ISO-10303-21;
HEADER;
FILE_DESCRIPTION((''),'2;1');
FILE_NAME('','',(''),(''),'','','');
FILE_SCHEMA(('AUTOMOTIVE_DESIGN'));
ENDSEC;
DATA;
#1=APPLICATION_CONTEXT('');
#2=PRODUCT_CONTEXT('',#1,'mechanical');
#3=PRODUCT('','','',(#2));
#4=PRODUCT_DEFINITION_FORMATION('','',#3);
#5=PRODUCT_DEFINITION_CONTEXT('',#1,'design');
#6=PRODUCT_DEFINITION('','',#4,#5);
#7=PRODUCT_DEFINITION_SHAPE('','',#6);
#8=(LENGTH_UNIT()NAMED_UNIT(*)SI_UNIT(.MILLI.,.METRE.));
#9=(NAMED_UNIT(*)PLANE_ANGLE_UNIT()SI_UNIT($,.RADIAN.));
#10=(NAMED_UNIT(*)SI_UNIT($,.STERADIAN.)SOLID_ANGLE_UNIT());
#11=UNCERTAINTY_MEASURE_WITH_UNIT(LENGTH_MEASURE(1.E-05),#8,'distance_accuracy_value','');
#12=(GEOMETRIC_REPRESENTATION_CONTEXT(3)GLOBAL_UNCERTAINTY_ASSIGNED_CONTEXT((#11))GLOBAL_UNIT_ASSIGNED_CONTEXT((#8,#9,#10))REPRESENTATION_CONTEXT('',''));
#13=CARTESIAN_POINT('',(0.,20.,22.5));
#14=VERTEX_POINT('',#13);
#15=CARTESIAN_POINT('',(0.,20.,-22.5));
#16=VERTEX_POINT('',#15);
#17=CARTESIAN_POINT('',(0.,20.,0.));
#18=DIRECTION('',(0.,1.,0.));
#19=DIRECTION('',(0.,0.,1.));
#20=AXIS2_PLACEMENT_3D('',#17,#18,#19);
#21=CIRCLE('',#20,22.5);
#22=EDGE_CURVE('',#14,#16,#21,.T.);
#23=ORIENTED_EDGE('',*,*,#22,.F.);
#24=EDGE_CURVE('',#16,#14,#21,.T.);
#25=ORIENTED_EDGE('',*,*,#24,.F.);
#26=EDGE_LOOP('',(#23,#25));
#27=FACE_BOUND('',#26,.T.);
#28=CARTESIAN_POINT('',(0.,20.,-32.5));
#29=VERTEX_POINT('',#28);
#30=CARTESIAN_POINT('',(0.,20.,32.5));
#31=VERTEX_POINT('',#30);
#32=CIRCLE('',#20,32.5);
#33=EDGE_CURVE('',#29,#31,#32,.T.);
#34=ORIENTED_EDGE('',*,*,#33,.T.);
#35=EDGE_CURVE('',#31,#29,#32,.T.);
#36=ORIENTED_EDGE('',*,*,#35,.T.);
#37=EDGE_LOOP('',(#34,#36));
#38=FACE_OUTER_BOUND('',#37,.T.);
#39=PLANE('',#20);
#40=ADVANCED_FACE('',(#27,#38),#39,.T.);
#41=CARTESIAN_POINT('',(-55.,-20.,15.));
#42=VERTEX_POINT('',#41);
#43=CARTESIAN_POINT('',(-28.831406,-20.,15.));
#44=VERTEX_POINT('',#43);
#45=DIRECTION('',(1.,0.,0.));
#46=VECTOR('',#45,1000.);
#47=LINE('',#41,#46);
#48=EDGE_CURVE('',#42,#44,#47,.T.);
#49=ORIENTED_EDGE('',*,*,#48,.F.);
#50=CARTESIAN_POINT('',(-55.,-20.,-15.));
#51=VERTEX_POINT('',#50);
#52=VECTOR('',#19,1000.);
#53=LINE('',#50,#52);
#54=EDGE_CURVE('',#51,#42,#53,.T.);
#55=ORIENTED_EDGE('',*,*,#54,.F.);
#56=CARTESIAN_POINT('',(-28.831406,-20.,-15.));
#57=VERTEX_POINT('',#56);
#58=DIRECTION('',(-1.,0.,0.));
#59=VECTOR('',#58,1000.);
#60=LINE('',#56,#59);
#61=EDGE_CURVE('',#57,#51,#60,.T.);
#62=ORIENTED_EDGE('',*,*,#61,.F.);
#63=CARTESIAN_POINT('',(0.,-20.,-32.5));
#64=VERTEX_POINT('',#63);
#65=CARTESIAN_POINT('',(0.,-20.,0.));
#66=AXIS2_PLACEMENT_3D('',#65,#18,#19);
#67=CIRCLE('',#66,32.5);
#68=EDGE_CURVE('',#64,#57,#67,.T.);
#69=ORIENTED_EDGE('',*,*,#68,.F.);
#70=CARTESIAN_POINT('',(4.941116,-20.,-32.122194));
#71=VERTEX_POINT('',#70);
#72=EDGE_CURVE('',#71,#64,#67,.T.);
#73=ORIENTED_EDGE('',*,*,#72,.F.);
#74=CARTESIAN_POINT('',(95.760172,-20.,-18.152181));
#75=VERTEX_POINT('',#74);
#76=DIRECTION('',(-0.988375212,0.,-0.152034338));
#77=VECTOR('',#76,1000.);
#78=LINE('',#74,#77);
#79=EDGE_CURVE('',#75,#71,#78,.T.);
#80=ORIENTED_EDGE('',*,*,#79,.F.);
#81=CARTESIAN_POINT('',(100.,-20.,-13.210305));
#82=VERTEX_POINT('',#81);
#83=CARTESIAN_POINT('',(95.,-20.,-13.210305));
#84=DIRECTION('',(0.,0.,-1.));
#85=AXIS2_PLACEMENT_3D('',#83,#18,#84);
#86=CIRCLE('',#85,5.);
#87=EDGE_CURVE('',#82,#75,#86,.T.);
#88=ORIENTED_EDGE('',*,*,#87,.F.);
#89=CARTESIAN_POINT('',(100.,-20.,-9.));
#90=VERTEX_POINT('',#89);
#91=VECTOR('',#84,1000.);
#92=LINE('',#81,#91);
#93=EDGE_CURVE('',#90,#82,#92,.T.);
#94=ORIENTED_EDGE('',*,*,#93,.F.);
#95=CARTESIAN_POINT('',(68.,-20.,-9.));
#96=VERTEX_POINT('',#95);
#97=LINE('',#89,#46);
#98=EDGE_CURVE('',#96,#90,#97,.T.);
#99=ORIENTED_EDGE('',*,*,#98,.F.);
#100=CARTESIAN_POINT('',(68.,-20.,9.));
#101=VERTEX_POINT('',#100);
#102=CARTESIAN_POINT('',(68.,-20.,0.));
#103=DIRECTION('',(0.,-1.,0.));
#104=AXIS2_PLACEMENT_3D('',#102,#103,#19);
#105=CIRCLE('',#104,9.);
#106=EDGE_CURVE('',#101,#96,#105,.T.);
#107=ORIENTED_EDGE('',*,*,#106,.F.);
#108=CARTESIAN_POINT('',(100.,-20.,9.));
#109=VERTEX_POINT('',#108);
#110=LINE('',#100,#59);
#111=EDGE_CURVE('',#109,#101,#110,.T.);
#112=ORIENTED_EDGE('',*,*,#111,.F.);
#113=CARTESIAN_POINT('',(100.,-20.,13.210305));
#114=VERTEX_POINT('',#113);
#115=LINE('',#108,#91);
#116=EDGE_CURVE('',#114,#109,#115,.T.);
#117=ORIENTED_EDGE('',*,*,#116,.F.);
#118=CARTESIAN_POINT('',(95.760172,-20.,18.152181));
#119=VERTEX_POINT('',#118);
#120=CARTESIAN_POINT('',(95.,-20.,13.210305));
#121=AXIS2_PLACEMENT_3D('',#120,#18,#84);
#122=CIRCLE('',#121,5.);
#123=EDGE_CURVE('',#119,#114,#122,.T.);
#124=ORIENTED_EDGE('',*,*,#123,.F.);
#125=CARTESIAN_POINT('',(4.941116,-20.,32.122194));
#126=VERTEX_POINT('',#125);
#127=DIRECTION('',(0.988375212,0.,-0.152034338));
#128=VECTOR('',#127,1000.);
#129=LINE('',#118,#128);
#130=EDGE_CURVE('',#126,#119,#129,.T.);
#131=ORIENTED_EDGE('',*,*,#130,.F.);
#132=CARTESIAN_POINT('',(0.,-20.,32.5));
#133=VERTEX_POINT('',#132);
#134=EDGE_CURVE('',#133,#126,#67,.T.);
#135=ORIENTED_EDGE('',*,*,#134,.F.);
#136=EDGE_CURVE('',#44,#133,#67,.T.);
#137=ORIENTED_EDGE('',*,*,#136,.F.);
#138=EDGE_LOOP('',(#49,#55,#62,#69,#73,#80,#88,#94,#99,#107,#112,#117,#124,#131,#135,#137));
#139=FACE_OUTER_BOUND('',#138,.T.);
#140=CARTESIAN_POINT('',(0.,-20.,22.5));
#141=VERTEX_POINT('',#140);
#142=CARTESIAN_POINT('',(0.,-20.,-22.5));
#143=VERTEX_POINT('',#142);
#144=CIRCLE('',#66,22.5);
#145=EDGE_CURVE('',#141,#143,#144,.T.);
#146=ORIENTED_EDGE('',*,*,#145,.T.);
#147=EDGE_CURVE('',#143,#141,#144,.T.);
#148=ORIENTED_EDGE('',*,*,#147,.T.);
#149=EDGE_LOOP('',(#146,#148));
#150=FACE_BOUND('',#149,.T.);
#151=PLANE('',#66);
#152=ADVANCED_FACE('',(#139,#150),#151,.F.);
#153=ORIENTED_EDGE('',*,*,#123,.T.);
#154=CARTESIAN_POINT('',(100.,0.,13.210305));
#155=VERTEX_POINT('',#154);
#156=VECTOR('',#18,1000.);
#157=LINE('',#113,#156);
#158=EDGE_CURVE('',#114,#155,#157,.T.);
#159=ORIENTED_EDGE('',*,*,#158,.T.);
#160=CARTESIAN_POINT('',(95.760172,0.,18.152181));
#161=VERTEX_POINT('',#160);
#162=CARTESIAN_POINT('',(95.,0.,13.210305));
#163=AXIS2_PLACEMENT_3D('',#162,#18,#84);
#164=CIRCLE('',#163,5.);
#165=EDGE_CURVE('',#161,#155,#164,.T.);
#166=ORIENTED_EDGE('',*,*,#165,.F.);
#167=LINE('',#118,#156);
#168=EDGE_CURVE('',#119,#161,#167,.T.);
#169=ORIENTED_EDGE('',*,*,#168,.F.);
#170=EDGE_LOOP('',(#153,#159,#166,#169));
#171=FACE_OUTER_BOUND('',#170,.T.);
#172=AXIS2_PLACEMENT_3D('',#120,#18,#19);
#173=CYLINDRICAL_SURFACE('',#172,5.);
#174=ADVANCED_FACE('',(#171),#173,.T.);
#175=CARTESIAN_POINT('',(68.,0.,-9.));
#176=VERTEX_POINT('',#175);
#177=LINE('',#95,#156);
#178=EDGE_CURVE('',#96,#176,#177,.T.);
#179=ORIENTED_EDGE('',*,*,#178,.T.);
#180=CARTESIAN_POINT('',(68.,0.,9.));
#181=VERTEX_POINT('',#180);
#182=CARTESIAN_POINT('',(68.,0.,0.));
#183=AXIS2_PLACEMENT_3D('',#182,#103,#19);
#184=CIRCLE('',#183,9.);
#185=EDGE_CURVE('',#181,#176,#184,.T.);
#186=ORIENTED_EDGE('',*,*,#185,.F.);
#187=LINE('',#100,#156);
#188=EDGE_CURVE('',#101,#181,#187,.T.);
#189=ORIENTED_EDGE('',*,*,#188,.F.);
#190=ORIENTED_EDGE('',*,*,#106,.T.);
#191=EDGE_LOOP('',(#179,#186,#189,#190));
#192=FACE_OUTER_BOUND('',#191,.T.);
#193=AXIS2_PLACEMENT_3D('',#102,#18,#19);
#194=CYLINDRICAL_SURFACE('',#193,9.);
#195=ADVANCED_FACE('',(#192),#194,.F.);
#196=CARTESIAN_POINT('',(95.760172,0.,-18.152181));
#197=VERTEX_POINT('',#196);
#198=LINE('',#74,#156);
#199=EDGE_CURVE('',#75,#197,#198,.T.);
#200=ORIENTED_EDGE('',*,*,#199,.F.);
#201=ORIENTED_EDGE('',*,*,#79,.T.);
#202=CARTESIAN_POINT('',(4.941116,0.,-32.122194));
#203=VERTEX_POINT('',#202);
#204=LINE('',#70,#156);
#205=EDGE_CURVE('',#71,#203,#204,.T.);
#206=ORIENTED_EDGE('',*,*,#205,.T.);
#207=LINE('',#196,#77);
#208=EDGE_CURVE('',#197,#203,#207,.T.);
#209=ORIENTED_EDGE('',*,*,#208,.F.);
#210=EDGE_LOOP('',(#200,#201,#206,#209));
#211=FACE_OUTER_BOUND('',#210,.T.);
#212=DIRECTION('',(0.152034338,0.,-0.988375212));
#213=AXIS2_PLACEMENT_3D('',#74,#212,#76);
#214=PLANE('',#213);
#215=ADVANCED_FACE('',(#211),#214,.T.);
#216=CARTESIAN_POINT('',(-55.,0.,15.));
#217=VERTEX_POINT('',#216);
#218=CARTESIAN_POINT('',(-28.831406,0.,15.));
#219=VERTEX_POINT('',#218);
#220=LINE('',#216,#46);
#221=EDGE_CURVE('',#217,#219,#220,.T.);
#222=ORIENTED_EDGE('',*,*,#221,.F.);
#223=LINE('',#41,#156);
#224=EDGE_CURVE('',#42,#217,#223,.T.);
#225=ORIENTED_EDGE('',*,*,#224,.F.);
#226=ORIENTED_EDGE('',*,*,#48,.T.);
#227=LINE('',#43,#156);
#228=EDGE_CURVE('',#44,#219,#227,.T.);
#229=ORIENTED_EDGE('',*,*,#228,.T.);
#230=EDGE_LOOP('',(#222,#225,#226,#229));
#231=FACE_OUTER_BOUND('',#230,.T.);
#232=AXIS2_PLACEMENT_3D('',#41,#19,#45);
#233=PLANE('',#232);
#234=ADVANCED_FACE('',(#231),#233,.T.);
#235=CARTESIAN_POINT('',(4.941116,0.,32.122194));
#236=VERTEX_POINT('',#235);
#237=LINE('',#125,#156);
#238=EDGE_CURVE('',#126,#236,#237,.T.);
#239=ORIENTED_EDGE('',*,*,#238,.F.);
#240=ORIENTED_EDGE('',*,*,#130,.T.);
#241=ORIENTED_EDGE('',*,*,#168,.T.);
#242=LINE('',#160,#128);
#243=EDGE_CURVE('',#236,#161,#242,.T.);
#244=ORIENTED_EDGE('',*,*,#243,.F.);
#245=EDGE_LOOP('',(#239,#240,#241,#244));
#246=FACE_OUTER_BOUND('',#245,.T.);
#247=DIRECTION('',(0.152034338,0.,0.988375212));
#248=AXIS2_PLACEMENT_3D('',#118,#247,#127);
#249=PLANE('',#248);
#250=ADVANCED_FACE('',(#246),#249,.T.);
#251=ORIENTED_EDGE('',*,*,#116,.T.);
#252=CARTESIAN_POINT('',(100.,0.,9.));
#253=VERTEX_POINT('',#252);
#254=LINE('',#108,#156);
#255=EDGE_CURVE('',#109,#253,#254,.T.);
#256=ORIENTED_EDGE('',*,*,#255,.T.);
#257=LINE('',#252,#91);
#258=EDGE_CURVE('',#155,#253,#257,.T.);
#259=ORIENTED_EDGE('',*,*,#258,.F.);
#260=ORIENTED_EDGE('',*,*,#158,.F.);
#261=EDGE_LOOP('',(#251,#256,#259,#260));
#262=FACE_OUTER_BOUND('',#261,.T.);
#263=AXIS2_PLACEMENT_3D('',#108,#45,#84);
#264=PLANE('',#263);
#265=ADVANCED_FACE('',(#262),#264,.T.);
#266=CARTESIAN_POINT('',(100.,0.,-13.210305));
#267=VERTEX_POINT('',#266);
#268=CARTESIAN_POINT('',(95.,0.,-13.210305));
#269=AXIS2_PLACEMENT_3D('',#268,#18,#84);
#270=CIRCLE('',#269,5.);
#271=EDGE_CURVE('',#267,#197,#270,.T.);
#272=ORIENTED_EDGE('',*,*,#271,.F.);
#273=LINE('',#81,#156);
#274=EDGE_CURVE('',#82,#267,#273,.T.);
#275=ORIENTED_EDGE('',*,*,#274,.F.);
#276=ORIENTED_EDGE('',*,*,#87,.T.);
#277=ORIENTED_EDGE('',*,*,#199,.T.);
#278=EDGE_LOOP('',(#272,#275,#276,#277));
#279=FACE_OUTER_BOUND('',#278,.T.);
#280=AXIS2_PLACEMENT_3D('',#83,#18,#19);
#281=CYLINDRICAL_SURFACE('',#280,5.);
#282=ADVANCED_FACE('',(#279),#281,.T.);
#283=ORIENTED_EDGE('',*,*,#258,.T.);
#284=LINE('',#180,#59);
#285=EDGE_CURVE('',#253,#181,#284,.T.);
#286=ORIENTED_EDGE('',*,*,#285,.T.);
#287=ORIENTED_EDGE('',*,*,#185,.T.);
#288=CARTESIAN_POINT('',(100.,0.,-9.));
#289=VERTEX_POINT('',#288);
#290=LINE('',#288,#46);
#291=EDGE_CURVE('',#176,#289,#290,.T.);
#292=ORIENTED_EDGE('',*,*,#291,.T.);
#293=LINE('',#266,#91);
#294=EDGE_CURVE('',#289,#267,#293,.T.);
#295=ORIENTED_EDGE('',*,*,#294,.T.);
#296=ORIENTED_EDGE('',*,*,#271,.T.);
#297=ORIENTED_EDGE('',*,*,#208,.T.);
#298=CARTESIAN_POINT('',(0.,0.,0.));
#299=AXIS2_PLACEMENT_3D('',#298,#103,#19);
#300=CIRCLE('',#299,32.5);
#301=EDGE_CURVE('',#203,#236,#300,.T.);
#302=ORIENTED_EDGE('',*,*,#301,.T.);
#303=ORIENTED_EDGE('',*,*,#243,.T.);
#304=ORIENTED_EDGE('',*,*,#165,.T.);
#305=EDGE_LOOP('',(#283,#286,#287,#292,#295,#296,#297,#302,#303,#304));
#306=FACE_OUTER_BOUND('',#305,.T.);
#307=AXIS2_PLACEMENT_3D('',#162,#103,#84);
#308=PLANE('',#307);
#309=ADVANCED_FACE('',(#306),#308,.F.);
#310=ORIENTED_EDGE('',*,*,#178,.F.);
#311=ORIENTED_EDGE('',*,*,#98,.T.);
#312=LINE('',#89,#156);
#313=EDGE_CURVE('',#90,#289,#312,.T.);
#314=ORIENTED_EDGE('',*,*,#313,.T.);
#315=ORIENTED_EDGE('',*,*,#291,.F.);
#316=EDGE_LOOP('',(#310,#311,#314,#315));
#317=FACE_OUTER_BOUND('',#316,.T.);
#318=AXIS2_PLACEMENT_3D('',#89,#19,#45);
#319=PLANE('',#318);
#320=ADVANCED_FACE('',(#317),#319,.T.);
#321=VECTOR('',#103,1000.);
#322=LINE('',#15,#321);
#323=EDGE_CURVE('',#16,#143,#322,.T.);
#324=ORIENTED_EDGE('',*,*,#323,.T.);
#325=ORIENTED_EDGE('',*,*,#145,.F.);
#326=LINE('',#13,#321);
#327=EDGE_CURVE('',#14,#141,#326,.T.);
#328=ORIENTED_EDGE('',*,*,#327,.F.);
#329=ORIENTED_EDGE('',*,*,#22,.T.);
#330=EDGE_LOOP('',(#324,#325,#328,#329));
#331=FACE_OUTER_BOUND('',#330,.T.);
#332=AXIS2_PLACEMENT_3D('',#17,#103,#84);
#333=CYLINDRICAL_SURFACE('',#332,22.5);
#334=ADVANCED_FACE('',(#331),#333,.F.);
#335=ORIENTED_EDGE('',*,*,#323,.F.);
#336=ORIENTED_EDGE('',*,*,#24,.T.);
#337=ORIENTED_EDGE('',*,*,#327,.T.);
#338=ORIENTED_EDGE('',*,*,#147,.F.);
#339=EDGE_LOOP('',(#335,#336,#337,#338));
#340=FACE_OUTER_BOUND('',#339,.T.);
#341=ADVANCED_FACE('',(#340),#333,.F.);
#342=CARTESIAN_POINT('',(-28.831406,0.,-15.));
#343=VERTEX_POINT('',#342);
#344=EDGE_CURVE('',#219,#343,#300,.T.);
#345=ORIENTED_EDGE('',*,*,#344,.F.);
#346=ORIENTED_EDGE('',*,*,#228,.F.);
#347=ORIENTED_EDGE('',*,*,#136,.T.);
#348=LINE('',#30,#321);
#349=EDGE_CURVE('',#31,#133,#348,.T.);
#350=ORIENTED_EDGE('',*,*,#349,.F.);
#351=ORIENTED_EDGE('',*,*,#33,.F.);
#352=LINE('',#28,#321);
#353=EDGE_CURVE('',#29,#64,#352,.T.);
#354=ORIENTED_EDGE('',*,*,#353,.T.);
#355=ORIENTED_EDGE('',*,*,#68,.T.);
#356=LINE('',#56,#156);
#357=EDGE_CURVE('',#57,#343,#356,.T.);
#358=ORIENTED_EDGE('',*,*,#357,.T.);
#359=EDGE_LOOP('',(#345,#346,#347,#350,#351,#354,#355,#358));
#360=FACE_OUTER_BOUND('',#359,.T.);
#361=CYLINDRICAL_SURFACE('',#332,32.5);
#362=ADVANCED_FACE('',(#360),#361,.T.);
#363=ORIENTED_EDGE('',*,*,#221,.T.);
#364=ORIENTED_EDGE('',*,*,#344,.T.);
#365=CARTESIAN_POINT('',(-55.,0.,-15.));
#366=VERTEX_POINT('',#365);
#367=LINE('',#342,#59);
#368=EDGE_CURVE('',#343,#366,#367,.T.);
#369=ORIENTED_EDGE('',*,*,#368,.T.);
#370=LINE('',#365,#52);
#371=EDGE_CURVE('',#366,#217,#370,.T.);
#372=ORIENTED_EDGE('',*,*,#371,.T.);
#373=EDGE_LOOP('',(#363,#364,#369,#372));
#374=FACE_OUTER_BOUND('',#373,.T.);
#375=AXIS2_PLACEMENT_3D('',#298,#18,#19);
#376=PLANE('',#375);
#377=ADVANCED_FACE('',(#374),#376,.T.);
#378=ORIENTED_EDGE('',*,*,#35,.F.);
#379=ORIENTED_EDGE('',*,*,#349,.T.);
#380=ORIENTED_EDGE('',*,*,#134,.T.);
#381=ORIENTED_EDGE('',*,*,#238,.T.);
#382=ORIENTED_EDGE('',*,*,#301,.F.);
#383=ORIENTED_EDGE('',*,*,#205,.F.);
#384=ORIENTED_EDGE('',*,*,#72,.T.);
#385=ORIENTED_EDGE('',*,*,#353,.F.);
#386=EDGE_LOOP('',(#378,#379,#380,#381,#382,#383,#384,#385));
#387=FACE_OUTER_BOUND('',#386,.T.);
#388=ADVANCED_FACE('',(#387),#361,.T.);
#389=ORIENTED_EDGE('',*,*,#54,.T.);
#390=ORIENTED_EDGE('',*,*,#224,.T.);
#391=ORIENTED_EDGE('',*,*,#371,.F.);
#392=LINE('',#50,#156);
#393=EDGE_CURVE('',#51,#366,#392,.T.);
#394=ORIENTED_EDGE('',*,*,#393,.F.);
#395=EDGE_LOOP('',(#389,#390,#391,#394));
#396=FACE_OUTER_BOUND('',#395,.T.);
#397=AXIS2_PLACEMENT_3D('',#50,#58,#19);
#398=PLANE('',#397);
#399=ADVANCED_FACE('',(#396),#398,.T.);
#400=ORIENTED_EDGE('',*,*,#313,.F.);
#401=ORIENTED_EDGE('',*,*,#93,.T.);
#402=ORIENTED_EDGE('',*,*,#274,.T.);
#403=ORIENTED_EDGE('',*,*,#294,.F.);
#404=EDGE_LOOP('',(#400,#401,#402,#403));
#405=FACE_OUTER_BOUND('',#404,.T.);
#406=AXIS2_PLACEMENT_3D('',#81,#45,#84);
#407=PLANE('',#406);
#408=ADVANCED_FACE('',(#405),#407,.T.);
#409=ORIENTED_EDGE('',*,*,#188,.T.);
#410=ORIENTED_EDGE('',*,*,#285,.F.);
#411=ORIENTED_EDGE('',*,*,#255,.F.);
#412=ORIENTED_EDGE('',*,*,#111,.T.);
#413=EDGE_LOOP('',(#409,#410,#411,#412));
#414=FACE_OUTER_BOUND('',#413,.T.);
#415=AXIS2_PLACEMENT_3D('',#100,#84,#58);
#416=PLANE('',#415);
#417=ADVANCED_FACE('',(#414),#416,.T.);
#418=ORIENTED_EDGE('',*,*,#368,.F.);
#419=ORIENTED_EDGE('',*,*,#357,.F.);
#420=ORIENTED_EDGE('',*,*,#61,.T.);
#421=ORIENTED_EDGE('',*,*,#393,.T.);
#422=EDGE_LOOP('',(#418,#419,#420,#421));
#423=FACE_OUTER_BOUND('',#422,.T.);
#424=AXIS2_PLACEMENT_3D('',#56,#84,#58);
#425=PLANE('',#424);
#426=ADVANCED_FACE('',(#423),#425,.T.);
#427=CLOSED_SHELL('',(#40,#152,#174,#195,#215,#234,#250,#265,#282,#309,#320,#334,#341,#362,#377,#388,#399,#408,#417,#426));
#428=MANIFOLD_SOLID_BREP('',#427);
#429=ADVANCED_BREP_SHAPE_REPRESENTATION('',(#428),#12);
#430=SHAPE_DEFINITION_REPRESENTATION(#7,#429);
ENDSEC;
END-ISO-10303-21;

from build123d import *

# Parameters (mm, degrees)
HUB_RING_SKETCH_R     = 32.5
HUB_RING_SKETCH_R_2   = 22.5
HUB_RING_65X_45_DEPTH = 20
FORK_ARM_DEPTH        = 20
REAR_TAB_DEPTH        = 20


with BuildPart() as part:
    # Hub Ring Sketch → Hub Ring Ø65xØ45 (new, symmetric)
    with BuildSketch(Plane(origin=(0, 0, 0), x_dir=(1, 0, 0), z_dir=(0, 1, 0))):
        with Locations(Location((0, 0, 0), (0, 0, 270))):
            Circle(HUB_RING_SKETCH_R)
        with Locations(Location((0, 0, 0), (0, 0, 270))):
            Circle(HUB_RING_SKETCH_R_2, mode=Mode.SUBTRACT)
    extrude(amount=HUB_RING_65X_45_DEPTH, both=True)

    # Fork Arm Sketch → Fork Arm (add)
    with BuildSketch(Plane(origin=(0, 0, 0), x_dir=(1, 0, 0), z_dir=(0, 1, 0))):
        with BuildLine():
            Line((95.760171689, 18.152180955), (4.941115981, 32.122194397))
            ThreePointArc((4.941115981, 32.122194397), (32.5, 0), (4.941115981, -32.122194397))
            Line((4.941115981, -32.122194397), (95.760171689, -18.152180955))
            ThreePointArc((95.760171689, -18.152180955), (98.794789747, -16.466003095), (100, -13.210304894))
            Line((100, -13.210304894), (100, -9))
            Line((100, -9), (68, -9))
            ThreePointArc((68, -9), (59, 0), (68, 9))
            Line((68, 9), (100, 9))
            Line((100, 9), (100, 13.210304894))
            ThreePointArc((100, 13.210304894), (98.794789747, 16.466003095), (95.760171689, 18.152180955))
        make_face()
    extrude(amount=-FORK_ARM_DEPTH)

    # Rear Tab Sketch → Rear Tab (add)
    with BuildSketch(Plane(origin=(0, 0, 0), x_dir=(1, 0, 0), z_dir=(0, 1, 0))):
        with BuildLine():
            Line((-28.831406487, 15), (-55, 15))
            Line((-55, 15), (-55, -15))
            Line((-55, -15), (-28.831406487, -15))
            ThreePointArc((-28.831406487, -15), (-32.5, 0), (-28.831406487, 15))
        make_face()
    extrude(amount=-REAR_TAB_DEPTH)


solid = part.part
